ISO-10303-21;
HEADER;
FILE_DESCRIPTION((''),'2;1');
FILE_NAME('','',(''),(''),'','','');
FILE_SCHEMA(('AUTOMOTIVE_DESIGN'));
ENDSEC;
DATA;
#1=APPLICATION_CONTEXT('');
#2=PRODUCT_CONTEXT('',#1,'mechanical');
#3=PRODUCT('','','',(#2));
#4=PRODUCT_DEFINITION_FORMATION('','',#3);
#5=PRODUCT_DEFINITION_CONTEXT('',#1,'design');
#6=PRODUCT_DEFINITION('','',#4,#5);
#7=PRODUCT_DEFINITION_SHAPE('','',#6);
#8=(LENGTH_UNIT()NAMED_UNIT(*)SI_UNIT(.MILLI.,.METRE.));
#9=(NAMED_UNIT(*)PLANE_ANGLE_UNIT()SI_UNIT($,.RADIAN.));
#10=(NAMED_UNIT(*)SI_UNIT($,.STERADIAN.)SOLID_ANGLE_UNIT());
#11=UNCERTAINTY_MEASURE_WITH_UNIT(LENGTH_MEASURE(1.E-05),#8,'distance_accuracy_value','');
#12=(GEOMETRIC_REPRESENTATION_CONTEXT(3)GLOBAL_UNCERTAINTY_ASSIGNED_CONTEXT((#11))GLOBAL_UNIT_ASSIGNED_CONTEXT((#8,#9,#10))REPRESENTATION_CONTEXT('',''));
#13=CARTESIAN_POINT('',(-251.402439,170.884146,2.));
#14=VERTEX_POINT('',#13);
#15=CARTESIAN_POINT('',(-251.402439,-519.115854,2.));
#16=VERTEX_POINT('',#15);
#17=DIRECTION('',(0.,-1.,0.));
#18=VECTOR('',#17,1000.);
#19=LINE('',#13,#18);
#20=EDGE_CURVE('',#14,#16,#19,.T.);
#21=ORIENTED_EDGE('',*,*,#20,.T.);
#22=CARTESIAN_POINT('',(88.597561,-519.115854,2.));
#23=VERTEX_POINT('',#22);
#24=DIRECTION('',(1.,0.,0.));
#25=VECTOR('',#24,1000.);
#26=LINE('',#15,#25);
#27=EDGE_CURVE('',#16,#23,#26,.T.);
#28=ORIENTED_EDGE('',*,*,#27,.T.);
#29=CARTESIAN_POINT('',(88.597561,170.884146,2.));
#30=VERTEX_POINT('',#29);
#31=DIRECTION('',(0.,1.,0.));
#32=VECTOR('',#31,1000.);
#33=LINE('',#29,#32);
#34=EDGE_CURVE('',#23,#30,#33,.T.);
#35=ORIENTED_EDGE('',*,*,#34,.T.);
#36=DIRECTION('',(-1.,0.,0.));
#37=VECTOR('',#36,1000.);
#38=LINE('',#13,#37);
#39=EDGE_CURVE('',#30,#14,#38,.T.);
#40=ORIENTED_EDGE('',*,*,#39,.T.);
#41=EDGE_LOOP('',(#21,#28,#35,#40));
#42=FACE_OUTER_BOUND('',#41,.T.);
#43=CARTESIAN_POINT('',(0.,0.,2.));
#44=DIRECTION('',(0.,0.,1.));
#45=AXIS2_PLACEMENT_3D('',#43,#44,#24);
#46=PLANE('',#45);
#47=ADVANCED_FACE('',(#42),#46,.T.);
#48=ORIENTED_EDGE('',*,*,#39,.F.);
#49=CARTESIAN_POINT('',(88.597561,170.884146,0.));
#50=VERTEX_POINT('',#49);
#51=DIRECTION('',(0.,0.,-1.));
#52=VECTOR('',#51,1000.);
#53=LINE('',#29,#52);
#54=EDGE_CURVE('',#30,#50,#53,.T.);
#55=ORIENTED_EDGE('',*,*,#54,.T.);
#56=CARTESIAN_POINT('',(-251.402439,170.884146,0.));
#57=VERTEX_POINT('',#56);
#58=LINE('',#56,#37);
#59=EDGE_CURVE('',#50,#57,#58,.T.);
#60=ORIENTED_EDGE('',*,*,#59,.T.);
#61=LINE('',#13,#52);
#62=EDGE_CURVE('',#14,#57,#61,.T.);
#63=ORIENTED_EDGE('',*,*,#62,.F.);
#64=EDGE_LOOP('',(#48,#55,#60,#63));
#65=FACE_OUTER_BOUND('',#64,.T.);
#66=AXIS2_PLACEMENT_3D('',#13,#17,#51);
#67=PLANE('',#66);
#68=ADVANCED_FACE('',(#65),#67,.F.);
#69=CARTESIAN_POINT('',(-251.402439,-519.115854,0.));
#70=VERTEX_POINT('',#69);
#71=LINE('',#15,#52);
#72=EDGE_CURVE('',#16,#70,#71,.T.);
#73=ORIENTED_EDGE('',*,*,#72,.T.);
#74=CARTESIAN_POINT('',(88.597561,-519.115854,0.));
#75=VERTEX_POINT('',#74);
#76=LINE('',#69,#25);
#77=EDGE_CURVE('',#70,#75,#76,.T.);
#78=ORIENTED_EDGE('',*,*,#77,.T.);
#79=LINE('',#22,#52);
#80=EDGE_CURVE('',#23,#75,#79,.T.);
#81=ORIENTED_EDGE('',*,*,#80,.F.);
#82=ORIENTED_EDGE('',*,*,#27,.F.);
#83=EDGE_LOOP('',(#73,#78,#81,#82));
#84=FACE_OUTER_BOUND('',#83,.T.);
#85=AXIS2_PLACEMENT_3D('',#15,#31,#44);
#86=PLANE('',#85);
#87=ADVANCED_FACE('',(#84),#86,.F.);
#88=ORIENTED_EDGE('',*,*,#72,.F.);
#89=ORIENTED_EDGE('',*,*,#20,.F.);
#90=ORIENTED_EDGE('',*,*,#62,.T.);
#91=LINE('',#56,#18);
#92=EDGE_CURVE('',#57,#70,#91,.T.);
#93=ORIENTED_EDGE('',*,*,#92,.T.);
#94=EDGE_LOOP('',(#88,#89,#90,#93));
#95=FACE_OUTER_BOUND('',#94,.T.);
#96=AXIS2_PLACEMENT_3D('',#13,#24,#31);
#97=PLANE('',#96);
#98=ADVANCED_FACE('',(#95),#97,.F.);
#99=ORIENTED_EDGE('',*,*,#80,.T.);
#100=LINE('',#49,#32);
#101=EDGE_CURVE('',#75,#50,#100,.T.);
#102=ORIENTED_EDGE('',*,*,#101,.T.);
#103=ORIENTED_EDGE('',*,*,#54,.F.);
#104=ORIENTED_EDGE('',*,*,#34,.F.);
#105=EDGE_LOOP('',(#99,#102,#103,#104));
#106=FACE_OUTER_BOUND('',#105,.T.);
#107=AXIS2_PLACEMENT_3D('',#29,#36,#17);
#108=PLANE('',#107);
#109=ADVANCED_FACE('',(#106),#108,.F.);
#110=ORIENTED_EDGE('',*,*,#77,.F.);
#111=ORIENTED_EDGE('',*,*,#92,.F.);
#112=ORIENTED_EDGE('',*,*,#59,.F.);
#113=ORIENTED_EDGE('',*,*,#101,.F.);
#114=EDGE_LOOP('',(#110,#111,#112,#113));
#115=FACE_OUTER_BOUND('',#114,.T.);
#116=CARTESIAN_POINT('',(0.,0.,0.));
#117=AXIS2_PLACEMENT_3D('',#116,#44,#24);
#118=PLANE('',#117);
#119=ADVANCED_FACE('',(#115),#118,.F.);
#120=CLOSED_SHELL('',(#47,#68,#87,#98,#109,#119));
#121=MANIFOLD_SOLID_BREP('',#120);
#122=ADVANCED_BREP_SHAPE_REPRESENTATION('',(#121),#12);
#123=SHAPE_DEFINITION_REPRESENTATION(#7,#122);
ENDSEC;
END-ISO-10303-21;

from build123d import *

# Parameters (mm, degrees)
SKETCH_1_W      = 340
SKETCH_1_H      = 690
EXTRUDE_1_DEPTH = 2


with BuildPart() as part:
    # 草图1 → 凸台-拉伸1 (new body)
    with BuildSketch(Plane.XY):
        with Locations((-81.402439024, -174.115853659)):
            Rectangle(SKETCH_1_W, SKETCH_1_H)
    extrude(amount=EXTRUDE_1_DEPTH)


solid = part.part
